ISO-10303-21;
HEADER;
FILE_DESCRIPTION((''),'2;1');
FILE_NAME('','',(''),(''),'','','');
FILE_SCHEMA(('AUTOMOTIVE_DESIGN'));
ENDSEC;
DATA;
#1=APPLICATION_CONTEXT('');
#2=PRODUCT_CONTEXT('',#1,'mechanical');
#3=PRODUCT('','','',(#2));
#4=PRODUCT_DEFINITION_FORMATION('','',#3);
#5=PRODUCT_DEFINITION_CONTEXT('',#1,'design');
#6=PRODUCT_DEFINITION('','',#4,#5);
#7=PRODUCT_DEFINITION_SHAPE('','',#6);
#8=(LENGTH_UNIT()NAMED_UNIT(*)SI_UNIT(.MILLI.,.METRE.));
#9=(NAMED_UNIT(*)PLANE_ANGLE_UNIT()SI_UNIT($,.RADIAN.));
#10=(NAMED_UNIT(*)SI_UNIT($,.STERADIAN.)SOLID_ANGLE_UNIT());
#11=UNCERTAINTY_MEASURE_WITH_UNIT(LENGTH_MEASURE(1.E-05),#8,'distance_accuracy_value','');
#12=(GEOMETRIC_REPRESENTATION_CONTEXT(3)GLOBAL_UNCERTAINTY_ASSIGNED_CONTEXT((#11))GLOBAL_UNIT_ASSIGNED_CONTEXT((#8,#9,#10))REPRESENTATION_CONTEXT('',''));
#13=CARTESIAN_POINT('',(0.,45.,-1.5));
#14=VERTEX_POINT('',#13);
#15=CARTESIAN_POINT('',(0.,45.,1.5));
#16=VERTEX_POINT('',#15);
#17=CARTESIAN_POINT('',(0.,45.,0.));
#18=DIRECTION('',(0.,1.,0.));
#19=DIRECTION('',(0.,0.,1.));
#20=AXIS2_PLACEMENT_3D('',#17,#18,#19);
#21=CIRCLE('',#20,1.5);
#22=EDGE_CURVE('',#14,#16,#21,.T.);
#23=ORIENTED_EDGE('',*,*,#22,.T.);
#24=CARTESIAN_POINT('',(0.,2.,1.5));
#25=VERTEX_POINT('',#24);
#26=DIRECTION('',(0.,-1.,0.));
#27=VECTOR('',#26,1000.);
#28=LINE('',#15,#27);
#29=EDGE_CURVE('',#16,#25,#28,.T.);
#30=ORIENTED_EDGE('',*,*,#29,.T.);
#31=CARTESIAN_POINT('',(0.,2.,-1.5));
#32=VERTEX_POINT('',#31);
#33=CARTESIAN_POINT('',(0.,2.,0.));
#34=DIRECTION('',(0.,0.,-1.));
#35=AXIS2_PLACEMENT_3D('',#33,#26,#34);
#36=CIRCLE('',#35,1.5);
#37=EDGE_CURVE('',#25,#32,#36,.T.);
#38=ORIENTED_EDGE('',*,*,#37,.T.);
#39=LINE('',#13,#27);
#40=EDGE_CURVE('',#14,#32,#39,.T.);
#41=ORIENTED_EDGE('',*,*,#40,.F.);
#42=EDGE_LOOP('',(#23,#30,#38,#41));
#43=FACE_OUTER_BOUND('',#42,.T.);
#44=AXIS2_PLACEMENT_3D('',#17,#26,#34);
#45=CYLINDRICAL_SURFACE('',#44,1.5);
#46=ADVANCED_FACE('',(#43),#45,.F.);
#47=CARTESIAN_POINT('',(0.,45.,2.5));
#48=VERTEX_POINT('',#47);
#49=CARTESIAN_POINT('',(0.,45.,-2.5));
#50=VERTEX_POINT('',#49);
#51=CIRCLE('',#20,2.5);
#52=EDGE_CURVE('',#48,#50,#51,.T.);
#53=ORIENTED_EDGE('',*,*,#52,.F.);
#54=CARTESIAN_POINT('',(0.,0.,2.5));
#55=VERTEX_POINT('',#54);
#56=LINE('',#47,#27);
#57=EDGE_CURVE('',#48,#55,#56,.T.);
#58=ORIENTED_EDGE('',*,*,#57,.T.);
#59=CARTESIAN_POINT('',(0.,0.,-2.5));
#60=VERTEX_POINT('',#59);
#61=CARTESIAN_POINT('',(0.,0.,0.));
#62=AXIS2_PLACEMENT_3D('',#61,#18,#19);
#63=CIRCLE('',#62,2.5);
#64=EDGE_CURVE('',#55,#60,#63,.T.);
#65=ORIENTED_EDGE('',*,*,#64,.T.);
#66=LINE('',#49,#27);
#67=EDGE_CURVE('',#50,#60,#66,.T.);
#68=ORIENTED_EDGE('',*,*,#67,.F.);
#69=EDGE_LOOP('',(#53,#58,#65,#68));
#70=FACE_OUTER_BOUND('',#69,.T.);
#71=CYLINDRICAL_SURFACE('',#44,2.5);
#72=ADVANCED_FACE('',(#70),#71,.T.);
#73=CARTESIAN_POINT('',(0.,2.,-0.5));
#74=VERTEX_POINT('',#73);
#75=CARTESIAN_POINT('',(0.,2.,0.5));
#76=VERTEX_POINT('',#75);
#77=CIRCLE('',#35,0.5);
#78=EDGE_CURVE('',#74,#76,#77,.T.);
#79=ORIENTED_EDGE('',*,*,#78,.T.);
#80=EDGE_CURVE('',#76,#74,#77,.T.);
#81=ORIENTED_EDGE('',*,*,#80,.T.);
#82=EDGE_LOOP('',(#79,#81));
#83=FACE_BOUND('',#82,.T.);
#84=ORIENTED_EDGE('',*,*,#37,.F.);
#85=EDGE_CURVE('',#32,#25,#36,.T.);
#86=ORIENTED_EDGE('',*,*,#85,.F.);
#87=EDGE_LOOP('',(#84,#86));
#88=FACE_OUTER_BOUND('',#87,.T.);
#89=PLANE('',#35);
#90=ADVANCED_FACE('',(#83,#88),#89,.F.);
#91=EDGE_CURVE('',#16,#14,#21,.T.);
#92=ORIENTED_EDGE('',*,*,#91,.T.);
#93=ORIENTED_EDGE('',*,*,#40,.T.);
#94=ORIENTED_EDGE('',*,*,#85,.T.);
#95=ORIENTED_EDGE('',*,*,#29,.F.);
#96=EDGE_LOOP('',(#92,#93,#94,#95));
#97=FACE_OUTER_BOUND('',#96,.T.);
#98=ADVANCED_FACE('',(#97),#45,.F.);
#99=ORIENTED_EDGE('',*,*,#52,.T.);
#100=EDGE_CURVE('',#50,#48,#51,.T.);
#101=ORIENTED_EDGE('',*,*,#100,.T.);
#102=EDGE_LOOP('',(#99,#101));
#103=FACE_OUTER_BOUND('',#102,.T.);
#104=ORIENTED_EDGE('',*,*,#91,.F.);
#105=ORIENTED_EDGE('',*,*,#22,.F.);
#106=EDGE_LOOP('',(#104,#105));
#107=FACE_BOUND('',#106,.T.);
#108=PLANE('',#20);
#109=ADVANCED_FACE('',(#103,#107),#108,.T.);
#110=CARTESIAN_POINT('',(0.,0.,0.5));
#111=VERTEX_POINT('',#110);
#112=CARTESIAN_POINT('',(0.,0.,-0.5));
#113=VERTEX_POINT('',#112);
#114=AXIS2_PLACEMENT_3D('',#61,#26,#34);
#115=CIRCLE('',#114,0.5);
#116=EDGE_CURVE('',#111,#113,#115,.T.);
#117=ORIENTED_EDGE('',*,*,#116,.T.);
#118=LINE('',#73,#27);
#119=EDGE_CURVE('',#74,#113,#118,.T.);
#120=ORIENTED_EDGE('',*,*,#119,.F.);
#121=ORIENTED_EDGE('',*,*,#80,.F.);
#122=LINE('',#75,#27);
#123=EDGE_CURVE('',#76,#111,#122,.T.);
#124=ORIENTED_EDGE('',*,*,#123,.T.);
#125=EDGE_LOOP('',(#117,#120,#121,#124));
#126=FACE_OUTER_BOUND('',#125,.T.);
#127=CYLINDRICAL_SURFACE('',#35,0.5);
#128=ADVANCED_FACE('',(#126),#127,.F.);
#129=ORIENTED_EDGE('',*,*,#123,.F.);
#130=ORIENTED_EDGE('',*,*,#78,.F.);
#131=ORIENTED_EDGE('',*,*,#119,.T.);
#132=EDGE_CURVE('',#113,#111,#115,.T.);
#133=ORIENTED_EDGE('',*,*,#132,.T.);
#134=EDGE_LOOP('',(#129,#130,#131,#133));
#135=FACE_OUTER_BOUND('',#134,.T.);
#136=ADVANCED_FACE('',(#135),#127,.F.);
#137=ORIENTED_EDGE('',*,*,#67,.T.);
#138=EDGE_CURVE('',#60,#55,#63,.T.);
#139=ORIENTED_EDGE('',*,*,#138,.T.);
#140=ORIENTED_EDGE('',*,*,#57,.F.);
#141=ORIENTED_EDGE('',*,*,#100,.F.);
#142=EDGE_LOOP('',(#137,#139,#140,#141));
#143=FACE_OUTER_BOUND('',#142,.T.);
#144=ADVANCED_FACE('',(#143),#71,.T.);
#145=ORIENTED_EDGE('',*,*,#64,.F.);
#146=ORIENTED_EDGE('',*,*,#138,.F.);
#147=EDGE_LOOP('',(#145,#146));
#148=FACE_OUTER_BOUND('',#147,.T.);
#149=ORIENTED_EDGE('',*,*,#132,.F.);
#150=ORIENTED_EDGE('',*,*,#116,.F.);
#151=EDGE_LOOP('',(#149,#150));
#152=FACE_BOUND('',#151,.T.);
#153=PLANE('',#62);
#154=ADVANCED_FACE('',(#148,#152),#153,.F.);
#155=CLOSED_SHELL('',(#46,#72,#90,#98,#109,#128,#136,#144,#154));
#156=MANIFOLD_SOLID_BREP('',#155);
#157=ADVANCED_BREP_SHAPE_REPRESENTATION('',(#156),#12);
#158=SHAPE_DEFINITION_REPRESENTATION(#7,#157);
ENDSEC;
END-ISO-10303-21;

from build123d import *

# Parameters (mm, degrees)
SKETCH1_R           = 2.5
SKETCH1_R_2         = 1.5
BOSS_EXTRUDE1_DEPTH = 45
SKETCH2_R           = 1.5
SKETCH2_R_2         = 0.5
BOSS_EXTRUDE2_DEPTH = 2


with BuildPart() as part:
    # Sketch1 → Boss-Extrude1 (new body)
    with BuildSketch(Plane(origin=(0, 0, 0), x_dir=(1, 0, 0), z_dir=(0, 1, 0))):
        with Locations(Location((0, 0, 0), (0, 0, 90))):
            Circle(SKETCH1_R)
        with Locations(Location((0, 0, 0), (0, 0, 90))):
            Circle(SKETCH1_R_2, mode=Mode.SUBTRACT)
    extrude(amount=BOSS_EXTRUDE1_DEPTH)

    # Sketch2 → Boss-Extrude2 (add)
    with BuildSketch(Plane.XZ):
        with Locations(Location((0, 0, 0), (0, 0, 270))):
            Circle(SKETCH2_R)
        with Locations(Location((0, 0, 0), (0, 0, 270))):
            Circle(SKETCH2_R_2, mode=Mode.SUBTRACT)
    extrude(amount=-BOSS_EXTRUDE2_DEPTH)


solid = part.part
